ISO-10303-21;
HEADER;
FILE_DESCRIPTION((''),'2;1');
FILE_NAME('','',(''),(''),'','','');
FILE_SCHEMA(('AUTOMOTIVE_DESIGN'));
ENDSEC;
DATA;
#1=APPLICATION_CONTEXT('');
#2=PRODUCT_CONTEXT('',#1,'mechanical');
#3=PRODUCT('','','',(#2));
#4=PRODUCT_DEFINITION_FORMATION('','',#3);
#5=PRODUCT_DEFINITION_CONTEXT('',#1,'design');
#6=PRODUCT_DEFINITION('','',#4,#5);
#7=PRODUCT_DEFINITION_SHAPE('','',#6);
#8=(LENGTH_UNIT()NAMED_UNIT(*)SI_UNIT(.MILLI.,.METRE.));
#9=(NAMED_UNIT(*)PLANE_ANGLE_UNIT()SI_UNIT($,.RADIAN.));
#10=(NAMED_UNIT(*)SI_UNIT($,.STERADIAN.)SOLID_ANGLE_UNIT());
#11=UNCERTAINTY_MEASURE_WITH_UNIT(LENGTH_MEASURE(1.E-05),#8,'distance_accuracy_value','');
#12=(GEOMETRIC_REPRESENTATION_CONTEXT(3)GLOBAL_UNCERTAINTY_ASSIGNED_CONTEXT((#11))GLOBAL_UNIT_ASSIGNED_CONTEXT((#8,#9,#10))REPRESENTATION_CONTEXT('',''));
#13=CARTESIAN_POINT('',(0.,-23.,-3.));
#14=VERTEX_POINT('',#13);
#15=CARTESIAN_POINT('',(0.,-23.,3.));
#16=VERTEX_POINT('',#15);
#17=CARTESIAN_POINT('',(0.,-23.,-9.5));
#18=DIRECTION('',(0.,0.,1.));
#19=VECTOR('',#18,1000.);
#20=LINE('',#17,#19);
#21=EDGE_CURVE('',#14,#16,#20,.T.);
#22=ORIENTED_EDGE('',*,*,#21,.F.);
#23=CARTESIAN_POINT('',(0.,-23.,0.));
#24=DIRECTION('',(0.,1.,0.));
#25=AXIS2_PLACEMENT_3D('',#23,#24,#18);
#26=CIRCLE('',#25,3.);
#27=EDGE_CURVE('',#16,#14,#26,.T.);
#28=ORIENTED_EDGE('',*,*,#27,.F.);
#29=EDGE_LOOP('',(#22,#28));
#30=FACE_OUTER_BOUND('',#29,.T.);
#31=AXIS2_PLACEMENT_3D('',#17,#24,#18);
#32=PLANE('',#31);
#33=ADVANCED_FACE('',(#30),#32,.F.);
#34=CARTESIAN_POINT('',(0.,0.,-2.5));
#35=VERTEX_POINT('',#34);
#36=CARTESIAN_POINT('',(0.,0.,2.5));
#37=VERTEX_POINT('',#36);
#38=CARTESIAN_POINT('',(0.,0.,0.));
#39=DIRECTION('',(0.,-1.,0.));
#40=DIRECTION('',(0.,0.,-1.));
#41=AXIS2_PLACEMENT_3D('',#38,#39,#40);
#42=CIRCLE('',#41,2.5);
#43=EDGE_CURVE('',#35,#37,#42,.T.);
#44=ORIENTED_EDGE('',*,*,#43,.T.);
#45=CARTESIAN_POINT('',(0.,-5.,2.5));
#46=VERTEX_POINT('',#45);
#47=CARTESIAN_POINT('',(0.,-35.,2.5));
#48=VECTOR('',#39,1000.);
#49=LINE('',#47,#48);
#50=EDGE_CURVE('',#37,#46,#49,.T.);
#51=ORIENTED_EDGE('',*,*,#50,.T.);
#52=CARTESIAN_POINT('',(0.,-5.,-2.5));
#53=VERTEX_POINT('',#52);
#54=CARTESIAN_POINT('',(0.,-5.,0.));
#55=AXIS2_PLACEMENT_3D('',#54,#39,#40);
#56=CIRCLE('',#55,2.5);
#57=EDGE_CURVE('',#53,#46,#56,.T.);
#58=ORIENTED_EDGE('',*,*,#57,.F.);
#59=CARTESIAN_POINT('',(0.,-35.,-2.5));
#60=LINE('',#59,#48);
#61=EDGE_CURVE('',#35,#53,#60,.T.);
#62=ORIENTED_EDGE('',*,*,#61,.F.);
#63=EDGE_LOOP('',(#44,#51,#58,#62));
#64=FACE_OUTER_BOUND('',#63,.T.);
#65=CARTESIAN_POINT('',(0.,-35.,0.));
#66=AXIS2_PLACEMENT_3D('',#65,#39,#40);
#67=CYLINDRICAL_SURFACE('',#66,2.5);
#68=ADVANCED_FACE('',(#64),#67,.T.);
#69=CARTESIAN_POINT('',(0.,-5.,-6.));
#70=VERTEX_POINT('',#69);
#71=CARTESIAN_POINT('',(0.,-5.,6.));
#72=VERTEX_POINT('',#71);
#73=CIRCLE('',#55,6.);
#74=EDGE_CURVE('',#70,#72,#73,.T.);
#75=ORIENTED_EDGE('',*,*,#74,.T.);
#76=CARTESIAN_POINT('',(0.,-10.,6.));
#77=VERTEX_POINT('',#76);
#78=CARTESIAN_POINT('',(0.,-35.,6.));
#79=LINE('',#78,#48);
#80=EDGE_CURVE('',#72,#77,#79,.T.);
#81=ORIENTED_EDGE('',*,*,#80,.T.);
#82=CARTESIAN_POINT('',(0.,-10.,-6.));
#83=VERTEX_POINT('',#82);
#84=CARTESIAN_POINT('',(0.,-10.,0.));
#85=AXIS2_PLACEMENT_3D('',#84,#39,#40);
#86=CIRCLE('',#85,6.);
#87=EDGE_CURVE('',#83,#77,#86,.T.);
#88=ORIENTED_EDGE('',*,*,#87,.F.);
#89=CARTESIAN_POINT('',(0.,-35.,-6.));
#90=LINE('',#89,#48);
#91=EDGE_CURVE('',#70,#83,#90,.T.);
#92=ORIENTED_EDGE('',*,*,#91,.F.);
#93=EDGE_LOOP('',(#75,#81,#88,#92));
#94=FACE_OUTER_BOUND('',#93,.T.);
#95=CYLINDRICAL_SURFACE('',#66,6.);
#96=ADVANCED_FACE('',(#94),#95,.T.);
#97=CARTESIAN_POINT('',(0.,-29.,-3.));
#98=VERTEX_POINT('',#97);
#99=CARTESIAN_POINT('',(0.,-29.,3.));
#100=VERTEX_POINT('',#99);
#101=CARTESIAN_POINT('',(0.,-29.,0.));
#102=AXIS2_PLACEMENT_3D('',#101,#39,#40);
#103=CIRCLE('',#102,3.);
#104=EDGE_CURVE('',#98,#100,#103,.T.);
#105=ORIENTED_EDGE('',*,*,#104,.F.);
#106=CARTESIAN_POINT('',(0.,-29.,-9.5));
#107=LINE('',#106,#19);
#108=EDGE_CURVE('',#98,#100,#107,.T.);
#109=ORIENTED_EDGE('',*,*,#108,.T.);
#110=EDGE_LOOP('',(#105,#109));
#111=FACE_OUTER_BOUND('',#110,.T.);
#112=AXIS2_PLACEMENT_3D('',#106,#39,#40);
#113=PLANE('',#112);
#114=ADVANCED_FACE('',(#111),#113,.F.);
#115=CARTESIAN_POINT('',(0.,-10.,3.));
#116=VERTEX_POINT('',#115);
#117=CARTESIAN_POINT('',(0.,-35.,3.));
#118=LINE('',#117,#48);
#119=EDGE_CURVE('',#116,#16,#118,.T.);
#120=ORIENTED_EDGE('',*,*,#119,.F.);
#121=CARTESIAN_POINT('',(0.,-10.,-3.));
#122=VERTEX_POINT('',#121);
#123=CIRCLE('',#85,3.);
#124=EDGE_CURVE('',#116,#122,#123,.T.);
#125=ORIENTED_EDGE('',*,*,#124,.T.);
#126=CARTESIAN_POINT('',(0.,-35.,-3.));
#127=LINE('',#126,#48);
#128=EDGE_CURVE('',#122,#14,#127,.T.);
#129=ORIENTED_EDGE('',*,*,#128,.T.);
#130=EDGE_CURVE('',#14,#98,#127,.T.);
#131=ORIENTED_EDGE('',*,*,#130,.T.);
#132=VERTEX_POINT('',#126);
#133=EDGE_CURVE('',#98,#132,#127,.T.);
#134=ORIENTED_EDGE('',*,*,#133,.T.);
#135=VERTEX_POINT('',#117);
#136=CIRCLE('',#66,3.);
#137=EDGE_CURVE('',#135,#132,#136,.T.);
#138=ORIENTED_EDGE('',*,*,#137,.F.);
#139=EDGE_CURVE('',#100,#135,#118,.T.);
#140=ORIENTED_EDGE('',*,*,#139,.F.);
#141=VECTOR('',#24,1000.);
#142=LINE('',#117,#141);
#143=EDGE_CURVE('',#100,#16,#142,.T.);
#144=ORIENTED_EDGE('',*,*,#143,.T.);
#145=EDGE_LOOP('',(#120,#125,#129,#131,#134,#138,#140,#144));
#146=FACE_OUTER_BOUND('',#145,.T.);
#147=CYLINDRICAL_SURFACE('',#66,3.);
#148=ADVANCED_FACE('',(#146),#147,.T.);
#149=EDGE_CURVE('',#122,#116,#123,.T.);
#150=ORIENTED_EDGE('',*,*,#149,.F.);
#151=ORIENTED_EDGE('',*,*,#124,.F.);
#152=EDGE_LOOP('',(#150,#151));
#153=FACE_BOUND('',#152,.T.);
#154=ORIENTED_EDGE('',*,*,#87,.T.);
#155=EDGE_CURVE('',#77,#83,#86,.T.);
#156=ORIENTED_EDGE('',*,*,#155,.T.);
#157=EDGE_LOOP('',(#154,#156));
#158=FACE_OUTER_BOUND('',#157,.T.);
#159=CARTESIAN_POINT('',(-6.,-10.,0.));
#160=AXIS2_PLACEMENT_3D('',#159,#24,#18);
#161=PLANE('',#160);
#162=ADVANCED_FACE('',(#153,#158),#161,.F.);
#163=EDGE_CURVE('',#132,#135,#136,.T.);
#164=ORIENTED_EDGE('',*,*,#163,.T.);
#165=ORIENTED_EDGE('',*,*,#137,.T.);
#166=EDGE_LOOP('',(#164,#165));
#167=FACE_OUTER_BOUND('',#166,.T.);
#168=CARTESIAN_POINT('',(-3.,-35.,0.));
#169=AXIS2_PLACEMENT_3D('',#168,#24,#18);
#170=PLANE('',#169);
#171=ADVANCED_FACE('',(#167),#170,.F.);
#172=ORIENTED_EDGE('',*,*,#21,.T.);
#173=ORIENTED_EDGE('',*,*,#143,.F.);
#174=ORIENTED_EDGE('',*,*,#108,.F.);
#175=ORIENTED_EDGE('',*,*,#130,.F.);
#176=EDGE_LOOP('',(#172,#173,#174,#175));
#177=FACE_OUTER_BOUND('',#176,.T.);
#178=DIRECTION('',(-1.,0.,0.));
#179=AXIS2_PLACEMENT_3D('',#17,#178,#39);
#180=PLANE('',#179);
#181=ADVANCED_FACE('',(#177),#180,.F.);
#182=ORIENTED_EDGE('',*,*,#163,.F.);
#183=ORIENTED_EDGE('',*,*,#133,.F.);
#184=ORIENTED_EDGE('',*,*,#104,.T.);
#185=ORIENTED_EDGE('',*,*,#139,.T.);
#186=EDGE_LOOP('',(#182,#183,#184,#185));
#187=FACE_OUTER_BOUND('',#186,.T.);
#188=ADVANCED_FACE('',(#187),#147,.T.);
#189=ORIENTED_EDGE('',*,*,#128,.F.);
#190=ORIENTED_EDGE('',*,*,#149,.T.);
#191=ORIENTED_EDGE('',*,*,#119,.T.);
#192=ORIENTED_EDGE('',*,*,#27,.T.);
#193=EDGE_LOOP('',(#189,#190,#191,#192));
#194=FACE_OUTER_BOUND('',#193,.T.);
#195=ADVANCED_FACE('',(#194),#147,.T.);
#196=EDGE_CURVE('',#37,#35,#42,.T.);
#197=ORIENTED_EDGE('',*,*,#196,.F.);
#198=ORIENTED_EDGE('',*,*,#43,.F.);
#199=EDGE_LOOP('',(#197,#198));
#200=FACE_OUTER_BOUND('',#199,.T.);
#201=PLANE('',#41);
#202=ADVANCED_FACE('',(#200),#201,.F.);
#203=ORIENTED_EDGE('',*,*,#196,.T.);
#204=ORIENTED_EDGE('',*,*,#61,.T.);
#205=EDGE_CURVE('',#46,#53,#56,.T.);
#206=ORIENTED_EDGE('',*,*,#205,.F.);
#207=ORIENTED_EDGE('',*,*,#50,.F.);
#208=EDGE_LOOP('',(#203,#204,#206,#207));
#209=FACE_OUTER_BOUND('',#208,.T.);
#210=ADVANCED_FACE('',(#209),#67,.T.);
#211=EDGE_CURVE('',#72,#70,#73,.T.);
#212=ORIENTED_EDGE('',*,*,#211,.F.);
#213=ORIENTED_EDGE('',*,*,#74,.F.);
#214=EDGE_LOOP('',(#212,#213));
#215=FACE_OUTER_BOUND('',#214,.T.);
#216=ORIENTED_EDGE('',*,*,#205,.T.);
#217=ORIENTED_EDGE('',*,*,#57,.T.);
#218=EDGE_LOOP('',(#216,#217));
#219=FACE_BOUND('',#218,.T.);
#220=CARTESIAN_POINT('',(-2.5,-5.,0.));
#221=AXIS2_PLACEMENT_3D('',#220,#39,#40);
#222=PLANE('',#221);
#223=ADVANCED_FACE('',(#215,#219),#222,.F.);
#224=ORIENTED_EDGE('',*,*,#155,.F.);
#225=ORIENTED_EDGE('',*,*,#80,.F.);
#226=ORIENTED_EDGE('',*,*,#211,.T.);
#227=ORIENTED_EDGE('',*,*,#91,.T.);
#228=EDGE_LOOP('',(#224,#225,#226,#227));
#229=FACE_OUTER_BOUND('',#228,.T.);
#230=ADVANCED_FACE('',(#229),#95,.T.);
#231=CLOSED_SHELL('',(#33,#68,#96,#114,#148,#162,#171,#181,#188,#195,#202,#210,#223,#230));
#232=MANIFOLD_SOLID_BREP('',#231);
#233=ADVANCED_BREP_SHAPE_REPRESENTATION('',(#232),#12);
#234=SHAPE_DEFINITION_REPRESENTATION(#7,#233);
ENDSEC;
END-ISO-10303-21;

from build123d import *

# Parameters (mm, degrees)
SIDE_NOTCH_SKETCH_W  = 8.527366903
SIDE_NOTCH_SKETCH_H  = 6
SIDE_NOTCH_6X6_DEPTH = 9.5


with BuildPart() as part:
    # Pin Profile Sketch → Pin Body (revolve)
    with BuildSketch(Plane.XY, mode=Mode.PRIVATE) as pin_body_sk:
        Polygon((0, 0), (-2.5, 0), (-2.5, -5), (-6, -5), (-6, -10), (-3, -10), (-3, -35), (0, -35), align=None)
    revolve(pin_body_sk.sketch.rotate(Axis((0, -35, 0), (0, 1, 0)), 270), axis=Axis((0, -35, 0), (0, 1, 0)))

    # Side Notch Sketch → Side Notch 6x6 (cut, symmetric)
    with BuildSketch(Plane.XY):
        with Locations((4.263683452, -26)):
            Rectangle(SIDE_NOTCH_SKETCH_W, SIDE_NOTCH_SKETCH_H)
    extrude(amount=SIDE_NOTCH_6X6_DEPTH, both=True, mode=Mode.SUBTRACT)


solid = part.part
